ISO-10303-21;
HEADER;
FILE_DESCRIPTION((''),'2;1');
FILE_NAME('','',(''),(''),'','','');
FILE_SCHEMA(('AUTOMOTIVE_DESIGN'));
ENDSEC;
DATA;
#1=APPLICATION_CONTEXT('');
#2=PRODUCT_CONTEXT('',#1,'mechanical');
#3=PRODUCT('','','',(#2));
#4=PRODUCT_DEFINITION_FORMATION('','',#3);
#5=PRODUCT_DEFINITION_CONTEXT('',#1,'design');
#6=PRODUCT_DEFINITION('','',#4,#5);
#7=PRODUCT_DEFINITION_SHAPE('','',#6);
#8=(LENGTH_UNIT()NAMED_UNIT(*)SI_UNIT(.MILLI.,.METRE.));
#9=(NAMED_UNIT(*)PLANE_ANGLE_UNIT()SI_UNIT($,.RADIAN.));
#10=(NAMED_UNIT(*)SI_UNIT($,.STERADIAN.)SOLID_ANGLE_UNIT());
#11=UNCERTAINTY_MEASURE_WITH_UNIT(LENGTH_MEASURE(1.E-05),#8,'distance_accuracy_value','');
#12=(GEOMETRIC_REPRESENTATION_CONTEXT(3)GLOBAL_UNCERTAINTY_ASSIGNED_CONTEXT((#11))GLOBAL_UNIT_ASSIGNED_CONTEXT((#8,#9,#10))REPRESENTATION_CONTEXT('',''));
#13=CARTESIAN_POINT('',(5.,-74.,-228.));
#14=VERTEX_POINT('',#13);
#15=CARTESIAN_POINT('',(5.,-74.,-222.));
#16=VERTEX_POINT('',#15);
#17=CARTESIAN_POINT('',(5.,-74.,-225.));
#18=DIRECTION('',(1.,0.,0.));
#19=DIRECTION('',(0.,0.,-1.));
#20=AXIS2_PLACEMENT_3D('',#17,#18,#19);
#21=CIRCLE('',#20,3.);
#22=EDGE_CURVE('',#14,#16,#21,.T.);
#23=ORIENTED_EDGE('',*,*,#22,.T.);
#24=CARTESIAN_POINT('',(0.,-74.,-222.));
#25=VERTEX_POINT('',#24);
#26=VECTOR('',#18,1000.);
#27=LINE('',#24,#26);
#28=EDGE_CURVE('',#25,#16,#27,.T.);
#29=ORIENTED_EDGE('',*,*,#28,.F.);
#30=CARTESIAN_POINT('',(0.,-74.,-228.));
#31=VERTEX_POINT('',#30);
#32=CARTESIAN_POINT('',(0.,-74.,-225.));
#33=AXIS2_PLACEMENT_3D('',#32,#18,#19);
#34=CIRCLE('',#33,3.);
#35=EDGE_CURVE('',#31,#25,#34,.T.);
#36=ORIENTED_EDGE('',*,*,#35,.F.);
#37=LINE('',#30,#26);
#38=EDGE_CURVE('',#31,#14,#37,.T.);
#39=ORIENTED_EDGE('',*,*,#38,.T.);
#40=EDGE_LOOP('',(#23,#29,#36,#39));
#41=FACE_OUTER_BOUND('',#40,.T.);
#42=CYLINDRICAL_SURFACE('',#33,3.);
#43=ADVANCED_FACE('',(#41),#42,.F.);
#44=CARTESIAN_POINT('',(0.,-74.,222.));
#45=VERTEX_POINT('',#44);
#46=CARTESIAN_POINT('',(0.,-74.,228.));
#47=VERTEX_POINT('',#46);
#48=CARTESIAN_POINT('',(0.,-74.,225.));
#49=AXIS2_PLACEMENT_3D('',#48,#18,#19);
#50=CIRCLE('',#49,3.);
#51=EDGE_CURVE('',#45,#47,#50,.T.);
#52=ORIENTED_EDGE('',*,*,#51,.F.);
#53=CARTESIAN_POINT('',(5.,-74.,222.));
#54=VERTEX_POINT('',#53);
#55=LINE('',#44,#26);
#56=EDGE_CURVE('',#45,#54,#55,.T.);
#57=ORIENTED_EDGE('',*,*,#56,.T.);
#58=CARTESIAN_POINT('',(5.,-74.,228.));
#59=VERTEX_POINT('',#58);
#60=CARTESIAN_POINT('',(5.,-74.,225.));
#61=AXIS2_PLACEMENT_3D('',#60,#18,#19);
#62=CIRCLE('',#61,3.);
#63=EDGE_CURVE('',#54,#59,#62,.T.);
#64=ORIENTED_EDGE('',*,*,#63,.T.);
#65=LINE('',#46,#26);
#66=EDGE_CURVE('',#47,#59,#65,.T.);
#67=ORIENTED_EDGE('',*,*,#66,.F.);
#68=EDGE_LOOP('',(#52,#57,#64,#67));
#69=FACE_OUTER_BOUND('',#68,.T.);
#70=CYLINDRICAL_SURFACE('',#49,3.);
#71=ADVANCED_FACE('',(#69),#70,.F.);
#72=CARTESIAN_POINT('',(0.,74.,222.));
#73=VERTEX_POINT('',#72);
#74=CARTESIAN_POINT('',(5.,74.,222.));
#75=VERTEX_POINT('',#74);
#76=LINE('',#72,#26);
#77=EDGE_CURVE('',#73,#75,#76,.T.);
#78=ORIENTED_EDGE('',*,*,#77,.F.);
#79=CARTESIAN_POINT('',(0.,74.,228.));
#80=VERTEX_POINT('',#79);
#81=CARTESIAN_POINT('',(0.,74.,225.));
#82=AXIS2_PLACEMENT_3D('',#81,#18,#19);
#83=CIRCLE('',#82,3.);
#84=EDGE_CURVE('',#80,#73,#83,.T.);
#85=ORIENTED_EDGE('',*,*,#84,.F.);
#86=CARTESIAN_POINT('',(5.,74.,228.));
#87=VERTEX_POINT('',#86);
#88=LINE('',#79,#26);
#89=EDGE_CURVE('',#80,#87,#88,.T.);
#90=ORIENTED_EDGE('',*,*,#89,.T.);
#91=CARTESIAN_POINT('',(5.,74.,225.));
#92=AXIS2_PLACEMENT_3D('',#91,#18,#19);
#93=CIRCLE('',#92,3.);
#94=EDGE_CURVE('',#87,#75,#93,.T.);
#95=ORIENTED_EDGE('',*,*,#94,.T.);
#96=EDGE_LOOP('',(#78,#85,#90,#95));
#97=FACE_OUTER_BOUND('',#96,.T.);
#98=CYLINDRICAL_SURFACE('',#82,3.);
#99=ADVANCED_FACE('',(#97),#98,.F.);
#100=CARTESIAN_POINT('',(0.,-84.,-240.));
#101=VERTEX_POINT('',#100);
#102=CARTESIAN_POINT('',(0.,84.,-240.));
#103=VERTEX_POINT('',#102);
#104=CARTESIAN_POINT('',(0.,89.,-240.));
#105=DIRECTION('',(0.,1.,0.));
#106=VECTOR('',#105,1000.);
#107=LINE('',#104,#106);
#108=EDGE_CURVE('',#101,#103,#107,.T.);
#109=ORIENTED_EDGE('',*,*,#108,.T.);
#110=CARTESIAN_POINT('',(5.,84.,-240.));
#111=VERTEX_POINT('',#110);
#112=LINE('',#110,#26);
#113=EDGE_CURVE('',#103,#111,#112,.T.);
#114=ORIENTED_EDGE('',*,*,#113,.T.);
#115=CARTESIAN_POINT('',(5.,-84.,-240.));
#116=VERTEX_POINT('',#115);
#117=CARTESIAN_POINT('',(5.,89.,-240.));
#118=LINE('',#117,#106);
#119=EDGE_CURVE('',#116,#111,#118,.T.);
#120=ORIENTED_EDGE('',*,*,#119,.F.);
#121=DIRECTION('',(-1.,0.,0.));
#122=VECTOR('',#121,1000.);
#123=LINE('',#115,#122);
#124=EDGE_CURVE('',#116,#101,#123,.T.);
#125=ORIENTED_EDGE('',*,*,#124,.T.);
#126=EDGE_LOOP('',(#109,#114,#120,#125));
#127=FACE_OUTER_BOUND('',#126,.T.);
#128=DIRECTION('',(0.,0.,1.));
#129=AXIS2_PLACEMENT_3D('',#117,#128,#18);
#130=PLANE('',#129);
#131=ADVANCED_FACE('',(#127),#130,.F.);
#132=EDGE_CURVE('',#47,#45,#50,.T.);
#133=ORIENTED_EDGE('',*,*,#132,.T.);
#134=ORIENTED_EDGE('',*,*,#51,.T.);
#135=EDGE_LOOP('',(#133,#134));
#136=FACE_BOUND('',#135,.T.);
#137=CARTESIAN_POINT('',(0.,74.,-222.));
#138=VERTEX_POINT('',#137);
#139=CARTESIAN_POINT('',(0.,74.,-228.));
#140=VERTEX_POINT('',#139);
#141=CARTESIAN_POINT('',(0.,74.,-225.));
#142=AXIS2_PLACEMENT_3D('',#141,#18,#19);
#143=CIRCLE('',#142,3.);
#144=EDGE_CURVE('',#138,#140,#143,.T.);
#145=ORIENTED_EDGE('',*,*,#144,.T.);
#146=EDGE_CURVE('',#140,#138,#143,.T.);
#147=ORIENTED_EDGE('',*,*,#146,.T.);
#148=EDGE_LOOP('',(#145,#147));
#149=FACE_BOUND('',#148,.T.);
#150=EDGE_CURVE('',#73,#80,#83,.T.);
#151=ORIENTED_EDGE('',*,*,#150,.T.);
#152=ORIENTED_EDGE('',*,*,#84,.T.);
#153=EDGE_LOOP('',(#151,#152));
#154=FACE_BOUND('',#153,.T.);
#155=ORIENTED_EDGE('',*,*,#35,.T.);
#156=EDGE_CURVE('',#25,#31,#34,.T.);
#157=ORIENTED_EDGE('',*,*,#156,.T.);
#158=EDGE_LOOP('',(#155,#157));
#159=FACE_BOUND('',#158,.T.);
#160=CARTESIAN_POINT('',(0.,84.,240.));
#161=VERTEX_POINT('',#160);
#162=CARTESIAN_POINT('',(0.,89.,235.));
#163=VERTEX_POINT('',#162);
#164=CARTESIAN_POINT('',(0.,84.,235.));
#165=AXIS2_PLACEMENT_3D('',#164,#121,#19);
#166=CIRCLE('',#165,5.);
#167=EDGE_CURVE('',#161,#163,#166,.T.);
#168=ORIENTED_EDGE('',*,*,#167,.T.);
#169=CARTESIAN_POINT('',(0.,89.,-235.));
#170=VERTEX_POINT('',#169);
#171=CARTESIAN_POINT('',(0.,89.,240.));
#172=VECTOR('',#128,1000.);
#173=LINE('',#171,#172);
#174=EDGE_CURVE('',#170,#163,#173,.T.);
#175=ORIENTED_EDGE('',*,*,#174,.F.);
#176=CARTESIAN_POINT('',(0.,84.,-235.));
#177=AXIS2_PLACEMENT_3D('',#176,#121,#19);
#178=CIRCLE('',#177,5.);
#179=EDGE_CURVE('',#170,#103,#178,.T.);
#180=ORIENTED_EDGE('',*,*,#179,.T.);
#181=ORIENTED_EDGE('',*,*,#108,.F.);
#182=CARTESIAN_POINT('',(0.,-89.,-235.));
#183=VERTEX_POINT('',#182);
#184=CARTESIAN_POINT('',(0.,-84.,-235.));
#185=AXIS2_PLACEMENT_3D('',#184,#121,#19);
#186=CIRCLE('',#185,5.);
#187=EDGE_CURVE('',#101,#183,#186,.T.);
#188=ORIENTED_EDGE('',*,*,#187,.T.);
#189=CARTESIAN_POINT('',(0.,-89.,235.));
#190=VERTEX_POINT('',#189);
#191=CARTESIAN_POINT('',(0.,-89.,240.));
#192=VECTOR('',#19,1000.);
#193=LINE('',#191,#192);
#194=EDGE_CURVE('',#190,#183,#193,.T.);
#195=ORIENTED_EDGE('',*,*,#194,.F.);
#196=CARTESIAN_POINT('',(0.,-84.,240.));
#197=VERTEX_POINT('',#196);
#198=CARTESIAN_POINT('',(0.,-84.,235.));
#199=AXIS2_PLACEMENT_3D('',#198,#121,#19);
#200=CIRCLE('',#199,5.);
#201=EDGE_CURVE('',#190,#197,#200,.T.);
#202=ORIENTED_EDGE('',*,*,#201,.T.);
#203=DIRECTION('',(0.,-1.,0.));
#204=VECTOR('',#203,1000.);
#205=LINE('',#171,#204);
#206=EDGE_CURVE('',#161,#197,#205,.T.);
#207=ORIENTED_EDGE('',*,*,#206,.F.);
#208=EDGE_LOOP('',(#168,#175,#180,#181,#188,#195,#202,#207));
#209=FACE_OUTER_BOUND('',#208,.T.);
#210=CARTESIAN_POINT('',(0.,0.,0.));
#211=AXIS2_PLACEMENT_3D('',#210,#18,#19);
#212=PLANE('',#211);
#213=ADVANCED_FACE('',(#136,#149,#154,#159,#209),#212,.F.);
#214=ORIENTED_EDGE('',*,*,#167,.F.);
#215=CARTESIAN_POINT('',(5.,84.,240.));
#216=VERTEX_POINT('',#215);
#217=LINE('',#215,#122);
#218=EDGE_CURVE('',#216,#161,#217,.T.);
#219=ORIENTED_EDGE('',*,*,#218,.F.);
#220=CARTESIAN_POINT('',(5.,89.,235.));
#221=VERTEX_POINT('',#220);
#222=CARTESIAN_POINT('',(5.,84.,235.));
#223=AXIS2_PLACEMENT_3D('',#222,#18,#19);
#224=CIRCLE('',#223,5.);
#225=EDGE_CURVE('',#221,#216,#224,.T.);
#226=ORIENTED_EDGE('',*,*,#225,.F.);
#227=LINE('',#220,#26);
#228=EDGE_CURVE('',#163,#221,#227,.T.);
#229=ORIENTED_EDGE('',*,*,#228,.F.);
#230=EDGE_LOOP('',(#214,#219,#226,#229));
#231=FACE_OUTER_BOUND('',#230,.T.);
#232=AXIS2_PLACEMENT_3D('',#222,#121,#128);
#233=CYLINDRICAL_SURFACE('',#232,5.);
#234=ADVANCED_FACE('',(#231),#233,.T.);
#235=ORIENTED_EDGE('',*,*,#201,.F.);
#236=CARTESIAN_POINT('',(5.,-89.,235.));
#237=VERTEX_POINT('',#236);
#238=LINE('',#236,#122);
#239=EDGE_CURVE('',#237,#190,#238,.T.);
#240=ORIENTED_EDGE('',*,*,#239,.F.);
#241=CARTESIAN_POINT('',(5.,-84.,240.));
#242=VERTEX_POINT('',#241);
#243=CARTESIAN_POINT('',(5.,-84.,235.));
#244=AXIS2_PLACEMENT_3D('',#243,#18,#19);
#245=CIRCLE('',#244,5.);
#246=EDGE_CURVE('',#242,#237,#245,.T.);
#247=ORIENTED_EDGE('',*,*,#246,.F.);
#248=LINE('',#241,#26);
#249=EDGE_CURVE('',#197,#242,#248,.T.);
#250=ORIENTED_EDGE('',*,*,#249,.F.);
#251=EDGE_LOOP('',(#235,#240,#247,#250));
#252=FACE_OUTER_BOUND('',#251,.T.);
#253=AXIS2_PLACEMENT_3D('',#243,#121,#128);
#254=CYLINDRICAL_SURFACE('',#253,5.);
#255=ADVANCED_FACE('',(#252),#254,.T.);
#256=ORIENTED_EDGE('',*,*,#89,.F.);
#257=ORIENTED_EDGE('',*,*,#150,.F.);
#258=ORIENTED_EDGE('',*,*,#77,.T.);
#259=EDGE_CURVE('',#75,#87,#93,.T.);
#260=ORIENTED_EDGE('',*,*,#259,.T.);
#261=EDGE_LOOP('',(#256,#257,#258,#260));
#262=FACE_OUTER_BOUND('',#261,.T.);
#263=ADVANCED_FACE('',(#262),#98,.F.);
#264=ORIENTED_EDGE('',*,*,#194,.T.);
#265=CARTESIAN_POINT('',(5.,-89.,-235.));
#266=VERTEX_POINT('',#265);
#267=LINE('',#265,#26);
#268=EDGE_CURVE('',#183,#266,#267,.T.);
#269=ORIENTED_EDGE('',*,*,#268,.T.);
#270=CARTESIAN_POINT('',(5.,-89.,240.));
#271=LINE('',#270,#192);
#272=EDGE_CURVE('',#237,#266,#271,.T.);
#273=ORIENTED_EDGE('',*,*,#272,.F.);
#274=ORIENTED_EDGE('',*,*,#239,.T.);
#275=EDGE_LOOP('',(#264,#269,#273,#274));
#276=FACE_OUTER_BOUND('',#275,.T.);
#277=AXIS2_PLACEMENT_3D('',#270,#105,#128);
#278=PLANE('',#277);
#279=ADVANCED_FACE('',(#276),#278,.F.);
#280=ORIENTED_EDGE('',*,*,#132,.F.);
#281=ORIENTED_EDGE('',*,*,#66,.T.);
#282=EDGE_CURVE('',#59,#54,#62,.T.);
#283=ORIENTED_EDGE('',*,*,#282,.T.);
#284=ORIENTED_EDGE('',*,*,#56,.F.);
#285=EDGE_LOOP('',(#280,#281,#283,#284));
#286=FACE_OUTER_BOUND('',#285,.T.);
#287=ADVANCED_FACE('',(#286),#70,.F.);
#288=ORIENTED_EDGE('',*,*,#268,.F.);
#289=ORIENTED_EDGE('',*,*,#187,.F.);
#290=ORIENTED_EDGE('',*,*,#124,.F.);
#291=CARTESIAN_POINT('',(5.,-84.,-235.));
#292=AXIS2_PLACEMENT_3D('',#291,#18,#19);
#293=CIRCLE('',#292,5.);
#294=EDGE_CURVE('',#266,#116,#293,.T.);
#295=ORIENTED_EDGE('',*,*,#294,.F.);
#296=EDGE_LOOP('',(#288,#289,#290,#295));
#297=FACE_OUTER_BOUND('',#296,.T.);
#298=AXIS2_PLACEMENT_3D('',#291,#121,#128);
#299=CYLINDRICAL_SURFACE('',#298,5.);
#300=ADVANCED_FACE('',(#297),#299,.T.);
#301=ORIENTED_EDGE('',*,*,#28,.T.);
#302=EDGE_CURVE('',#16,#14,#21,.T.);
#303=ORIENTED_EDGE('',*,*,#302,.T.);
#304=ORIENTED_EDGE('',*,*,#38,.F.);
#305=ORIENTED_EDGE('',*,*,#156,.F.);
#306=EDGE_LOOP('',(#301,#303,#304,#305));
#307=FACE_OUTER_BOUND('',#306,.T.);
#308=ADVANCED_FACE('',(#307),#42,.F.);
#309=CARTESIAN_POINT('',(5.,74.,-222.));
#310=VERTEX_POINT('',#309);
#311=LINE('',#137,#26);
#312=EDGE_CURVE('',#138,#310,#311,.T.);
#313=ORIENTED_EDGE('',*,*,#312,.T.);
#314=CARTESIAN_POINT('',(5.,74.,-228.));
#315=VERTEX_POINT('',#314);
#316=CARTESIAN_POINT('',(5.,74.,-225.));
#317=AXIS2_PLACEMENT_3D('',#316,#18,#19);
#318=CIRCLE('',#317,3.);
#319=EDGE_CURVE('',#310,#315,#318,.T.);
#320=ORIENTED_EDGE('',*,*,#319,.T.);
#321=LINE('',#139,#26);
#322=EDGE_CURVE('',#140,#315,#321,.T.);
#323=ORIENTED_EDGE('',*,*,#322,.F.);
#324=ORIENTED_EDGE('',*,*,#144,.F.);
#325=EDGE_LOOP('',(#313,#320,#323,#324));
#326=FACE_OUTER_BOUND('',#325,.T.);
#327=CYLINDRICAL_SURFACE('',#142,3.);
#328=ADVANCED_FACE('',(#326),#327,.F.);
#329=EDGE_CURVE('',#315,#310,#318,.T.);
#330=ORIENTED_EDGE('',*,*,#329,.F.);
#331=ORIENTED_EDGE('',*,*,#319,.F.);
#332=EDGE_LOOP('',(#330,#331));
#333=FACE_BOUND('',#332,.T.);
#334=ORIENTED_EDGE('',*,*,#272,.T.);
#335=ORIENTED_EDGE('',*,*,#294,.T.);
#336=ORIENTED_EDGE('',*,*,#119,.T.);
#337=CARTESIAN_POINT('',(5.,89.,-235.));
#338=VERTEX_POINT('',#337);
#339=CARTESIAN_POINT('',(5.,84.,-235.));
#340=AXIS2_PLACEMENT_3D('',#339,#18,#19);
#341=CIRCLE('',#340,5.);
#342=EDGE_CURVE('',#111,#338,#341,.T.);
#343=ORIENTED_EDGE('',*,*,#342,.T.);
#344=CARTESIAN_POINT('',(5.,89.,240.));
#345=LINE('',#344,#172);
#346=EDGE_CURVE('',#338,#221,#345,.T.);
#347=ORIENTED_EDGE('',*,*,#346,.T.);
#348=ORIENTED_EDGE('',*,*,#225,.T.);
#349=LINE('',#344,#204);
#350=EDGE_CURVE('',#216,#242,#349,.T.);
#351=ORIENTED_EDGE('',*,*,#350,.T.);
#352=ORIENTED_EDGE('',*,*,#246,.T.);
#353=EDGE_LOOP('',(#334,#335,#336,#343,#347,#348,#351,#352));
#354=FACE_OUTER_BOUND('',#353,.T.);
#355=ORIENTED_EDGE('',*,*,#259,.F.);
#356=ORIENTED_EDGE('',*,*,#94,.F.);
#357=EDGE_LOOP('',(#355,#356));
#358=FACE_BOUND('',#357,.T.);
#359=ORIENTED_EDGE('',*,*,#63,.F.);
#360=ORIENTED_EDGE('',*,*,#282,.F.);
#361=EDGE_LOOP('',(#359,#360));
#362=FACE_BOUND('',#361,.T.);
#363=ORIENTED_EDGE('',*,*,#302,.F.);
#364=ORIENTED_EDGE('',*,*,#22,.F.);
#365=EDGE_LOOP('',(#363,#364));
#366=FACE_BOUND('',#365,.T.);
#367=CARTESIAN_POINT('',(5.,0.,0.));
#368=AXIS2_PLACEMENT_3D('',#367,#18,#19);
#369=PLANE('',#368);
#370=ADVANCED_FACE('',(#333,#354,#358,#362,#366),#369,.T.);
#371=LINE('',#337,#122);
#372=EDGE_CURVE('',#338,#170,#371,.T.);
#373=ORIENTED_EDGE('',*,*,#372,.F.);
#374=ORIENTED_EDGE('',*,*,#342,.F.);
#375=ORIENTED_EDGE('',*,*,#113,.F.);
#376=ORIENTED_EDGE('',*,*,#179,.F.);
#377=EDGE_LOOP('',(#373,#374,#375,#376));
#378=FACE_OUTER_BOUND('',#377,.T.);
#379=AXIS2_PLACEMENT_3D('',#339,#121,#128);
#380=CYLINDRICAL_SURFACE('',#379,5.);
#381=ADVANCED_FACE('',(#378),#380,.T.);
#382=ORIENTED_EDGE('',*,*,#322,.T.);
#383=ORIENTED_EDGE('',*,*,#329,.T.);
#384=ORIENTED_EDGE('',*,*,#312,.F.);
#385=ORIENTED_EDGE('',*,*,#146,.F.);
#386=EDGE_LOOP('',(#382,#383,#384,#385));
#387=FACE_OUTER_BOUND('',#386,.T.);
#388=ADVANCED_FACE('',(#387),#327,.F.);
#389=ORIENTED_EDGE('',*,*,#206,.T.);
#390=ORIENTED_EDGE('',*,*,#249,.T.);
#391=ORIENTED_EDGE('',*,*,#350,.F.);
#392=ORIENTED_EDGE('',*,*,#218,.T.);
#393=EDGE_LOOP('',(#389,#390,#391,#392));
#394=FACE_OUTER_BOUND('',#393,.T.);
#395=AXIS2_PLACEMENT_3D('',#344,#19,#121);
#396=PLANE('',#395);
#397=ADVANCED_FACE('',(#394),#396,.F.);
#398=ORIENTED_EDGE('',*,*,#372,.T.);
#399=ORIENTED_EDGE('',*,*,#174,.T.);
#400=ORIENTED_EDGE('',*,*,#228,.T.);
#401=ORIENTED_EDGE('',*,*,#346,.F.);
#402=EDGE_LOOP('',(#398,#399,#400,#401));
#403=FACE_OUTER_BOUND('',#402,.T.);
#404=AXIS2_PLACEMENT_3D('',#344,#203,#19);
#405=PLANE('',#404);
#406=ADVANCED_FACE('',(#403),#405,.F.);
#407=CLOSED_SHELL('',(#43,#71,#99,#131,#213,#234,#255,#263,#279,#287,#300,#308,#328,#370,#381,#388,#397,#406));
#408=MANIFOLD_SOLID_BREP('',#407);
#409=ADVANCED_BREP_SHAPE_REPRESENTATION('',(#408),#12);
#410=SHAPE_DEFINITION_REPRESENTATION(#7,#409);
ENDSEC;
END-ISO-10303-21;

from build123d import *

# Parameters (mm, degrees)
SKETCH_1_W          = 480
SKETCH_1_H          = 178
EXTRUDE_1_DEPTH     = 5
SKETCH_2_R          = 3
CUT_EXTRUDE_1_DEPTH = 257.019530505
FILLET_1_R          = 5


with BuildPart() as part:
    # 草图1 → 凸台-拉伸1 (new body)
    with BuildSketch(Plane(origin=(0, 0, 0), x_dir=(0, 0, -1), z_dir=(1, 0, 0))):
        Rectangle(SKETCH_1_W, SKETCH_1_H)
    extrude(amount=EXTRUDE_1_DEPTH)

    # 草图2 → 切除-拉伸1 (cut, through all)
    with BuildSketch(Plane(origin=(5, 0, 0), x_dir=(0, 0, -1), z_dir=(1, 0, 0))):
        with Locations((-225, 74)):
            Circle(SKETCH_2_R)
        with Locations((225, 74)):
            Circle(SKETCH_2_R)
        with Locations((-225, -74)):
            Circle(SKETCH_2_R)
        with Locations((225, -74)):
            Circle(SKETCH_2_R)
    extrude(amount=-CUT_EXTRUDE_1_DEPTH, mode=Mode.SUBTRACT)

    # 圆角1
    fillet_1_edges = [part.edges().sort_by_distance(p)[0] for p in [
        (2.5, 89, 240),
        (2.5, 89, -240),
        (2.5, -89, -240),
        (2.5, -89, 240),
    ]]
    fillet(fillet_1_edges, radius=FILLET_1_R)


solid = part.part
